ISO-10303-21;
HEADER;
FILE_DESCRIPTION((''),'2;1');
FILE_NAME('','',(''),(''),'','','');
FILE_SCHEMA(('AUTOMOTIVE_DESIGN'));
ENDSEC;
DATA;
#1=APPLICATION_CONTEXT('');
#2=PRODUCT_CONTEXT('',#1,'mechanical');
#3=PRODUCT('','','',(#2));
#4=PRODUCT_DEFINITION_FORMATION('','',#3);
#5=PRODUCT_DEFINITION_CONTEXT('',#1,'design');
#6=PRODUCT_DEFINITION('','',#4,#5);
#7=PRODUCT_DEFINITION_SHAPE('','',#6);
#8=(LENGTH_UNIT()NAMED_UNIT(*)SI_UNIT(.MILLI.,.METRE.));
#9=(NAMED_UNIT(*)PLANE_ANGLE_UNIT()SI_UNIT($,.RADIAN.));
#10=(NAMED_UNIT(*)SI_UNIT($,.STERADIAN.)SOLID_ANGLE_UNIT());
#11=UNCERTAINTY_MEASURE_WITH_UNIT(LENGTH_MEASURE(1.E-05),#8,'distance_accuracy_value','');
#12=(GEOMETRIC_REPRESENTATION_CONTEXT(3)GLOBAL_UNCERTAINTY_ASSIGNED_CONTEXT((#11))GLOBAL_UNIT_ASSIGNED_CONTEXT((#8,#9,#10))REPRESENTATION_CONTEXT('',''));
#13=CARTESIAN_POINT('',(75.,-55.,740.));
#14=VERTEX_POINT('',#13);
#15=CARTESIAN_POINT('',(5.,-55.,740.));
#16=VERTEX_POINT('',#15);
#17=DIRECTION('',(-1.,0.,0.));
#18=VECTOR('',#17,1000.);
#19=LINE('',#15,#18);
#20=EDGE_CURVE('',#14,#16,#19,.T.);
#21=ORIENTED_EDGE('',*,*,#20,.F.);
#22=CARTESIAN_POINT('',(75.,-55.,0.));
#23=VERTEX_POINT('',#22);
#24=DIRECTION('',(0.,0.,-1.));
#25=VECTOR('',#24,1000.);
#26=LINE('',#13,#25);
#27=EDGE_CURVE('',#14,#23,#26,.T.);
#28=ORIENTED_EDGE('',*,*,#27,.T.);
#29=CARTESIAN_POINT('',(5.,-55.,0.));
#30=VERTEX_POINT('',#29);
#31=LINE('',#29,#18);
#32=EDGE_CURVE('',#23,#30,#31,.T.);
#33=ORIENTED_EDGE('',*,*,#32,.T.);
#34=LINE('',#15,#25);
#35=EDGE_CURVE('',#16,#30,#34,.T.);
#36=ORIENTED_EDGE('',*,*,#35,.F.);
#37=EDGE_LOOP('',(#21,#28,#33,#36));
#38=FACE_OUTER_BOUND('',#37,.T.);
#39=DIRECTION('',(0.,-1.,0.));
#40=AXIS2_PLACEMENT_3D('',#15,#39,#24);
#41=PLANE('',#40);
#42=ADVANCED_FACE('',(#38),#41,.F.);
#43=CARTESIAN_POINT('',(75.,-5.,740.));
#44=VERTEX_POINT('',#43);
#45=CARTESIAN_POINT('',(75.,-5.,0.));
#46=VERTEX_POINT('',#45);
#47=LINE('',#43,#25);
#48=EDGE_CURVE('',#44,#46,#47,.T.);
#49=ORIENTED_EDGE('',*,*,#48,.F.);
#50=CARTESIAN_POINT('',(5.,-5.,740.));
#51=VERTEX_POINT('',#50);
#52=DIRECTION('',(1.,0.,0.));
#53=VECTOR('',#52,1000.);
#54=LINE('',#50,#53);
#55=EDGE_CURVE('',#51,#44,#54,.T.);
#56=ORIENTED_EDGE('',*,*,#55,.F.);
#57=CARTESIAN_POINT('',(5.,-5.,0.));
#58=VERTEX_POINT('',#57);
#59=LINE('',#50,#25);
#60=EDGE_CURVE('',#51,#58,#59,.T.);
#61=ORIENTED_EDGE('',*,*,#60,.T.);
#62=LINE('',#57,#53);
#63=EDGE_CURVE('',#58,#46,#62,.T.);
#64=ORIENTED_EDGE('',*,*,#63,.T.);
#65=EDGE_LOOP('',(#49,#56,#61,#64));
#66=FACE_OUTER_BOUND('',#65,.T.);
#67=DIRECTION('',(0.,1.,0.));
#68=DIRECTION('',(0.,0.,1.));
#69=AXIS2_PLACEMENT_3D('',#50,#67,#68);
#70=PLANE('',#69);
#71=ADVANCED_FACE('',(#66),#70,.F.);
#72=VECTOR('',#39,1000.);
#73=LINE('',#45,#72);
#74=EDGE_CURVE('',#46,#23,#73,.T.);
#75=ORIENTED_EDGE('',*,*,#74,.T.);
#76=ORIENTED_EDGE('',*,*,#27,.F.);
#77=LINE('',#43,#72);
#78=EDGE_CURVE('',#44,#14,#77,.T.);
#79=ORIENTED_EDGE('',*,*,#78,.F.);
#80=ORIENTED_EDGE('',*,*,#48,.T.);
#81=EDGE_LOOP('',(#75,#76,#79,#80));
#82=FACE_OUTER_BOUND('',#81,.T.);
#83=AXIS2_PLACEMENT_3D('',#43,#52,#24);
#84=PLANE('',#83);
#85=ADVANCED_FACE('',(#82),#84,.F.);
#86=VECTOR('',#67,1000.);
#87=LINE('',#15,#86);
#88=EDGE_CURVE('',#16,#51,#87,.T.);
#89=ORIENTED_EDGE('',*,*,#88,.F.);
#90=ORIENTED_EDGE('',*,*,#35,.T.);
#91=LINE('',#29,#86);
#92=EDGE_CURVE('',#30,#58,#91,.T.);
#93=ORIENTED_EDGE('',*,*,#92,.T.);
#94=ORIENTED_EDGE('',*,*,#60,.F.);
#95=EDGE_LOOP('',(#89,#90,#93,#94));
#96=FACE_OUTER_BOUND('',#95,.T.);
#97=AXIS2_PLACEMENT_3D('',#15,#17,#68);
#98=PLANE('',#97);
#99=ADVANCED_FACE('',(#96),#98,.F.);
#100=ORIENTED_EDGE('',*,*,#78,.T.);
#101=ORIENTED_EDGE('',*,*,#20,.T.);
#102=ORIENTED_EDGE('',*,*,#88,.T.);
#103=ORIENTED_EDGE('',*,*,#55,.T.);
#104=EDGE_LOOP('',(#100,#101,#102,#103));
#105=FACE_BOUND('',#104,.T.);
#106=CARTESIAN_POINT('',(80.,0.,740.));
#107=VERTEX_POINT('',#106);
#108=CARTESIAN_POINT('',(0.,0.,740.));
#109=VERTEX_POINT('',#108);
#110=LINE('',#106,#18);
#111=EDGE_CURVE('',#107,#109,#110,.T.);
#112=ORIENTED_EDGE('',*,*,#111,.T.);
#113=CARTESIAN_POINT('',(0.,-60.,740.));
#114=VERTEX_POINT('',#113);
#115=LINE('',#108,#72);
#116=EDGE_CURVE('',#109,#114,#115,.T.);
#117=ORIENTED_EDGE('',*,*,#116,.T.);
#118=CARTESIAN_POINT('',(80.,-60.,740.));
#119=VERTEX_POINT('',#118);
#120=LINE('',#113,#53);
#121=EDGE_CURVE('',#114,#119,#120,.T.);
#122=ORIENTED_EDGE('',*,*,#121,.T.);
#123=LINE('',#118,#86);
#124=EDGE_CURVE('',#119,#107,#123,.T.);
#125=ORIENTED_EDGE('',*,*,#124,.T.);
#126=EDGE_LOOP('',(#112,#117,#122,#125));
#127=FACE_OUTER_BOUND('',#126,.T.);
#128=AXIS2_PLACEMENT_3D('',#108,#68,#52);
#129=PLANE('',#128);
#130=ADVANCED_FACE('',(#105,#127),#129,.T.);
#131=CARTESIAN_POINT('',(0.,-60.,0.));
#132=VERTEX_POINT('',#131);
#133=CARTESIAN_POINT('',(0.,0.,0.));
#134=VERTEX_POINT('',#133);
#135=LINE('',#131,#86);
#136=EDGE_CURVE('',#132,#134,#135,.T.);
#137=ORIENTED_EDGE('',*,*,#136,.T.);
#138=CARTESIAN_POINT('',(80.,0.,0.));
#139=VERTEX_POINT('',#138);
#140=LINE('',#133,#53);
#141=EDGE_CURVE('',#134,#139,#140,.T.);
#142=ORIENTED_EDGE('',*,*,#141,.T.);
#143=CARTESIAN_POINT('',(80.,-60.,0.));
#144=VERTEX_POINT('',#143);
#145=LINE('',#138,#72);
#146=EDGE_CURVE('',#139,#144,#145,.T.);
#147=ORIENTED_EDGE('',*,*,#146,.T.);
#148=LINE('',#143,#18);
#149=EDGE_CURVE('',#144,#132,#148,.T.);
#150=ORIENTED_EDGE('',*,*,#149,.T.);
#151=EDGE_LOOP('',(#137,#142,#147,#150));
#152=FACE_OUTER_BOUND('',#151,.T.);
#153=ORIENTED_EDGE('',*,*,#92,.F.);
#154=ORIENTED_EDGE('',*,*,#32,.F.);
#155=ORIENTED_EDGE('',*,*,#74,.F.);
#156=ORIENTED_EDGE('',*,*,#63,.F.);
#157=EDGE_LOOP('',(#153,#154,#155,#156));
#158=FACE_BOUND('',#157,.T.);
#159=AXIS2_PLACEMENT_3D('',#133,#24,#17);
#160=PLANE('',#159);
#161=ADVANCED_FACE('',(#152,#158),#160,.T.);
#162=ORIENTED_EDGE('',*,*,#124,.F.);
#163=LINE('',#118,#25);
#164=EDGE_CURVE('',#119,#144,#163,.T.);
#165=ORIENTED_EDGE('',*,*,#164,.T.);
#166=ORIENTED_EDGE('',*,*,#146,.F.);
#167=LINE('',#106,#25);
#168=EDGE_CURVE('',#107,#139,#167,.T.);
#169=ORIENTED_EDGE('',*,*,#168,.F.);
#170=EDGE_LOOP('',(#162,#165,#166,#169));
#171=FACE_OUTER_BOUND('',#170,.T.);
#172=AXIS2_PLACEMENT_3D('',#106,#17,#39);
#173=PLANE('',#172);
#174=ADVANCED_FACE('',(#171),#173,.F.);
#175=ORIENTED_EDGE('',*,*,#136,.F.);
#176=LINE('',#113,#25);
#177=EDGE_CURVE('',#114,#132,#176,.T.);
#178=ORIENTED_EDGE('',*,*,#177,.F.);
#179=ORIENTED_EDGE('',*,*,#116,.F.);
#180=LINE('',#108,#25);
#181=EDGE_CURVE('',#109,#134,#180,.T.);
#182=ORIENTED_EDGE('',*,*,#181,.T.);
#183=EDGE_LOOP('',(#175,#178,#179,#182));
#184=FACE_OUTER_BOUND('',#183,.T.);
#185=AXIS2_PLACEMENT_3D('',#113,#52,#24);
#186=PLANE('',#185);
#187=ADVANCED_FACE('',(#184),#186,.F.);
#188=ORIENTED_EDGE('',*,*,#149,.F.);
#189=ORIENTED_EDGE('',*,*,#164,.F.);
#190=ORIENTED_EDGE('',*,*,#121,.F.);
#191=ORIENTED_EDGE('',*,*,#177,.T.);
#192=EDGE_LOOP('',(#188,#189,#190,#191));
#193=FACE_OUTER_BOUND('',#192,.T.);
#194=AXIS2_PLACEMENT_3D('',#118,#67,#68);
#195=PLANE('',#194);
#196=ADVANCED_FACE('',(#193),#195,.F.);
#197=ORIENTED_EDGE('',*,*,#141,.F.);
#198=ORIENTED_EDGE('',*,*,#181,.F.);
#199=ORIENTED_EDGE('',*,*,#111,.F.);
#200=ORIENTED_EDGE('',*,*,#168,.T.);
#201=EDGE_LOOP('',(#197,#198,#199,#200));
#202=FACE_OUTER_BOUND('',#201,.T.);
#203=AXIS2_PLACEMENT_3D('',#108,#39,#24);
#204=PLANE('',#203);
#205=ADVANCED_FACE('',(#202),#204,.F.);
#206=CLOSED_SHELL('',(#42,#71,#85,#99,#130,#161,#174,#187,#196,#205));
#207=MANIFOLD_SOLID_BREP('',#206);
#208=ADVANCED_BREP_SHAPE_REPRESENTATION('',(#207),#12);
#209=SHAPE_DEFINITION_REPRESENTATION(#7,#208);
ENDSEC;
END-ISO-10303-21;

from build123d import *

# Parameters (mm, degrees)
SKETCH_1_W          = 80
SKETCH_1_H          = 60
SKETCH_1_W_2        = 74
SKETCH_1_H_2        = 54
EXTRUDE_1_DEPTH     = 740
SKETCH_3_W          = 80
SKETCH_3_H          = 60
CUT_EXTRUDE_1_DEPTH = 25
SKETCH_4_W          = 80
SKETCH_4_H          = 60
CUT_EXTRUDE_2_DEPTH = 25
SKETCH_5_W          = 80
SKETCH_5_H          = 60
SKETCH_5_W_2        = 74
SKETCH_5_H_2        = 54
EXTRUDE_2_DEPTH     = 25
SKETCH_6_W          = 80
SKETCH_6_H          = 60
SKETCH_6_W_2        = 74
SKETCH_6_H_2        = 54
EXTRUDE_3_DEPTH     = 25
SKETCH_7_W          = 45
SKETCH_7_H          = 5
CUT_EXTRUDE_3_DEPTH = 80
EXTRUDE_4_DEPTH     = 45
EXTRUDE_5_DEPTH     = 45
SKETCH_10_W         = 74
SKETCH_10_H         = 54
SKETCH_10_W_2       = 70
SKETCH_10_H_2       = 50
EXTRUDE_6_DEPTH     = 740


with BuildPart() as part:
    # 草图1 → 凸台-拉伸1 (new body)
    with BuildSketch(Plane.XY):
        with Locations((40, -30)):
            Rectangle(SKETCH_1_W, SKETCH_1_H)
        with Locations((40, -30)):
            Rectangle(SKETCH_1_W_2, SKETCH_1_H_2, mode=Mode.SUBTRACT)
    extrude(amount=EXTRUDE_1_DEPTH)

    # 草图3 → 切除-拉伸1 (cut)
    with BuildSketch(Plane.XY.offset(740)):
        with Locations((40, -30)):
            Rectangle(SKETCH_3_W, SKETCH_3_H)
    extrude(amount=-CUT_EXTRUDE_1_DEPTH, mode=Mode.SUBTRACT)

    # 草图4 → 切除-拉伸2 (cut)
    with BuildSketch(Plane(origin=(0, 0, 0), x_dir=(-1, 0, 0), z_dir=(0, 0, -1))):
        with Locations((-40, -30)):
            Rectangle(SKETCH_4_W, SKETCH_4_H)
    extrude(amount=-CUT_EXTRUDE_2_DEPTH, mode=Mode.SUBTRACT)

    # 草图5 → 凸台-拉伸2 (add)
    with BuildSketch(Plane.XY.offset(715)):
        with Locations((40, -30)):
            Rectangle(SKETCH_5_W, SKETCH_5_H)
        with Locations((40, -30)):
            Rectangle(SKETCH_5_W_2, SKETCH_5_H_2, mode=Mode.SUBTRACT)
    extrude(amount=EXTRUDE_2_DEPTH)

    # 草图6 → 凸台-拉伸3 (add)
    with BuildSketch(Plane(origin=(0, 0, 25), x_dir=(-1, 0, 0), z_dir=(0, 0, -1))):
        with Locations((-40, -30)):
            Rectangle(SKETCH_6_W, SKETCH_6_H)
        with Locations((-40, -30)):
            Rectangle(SKETCH_6_W_2, SKETCH_6_H_2, mode=Mode.SUBTRACT)
    extrude(amount=EXTRUDE_3_DEPTH)

    # 草图7 → 切除-拉伸3 (cut)
    with BuildSketch(Plane(origin=(80, 0, 0), x_dir=(0, 0, -1), z_dir=(1, 0, 0))):
        with Locations((-717.5, -57.5)):
            Rectangle(SKETCH_7_W, SKETCH_7_H)
        with Locations((-22.5, -57.5)):
            Rectangle(SKETCH_7_W, SKETCH_7_H)
    extrude(amount=-CUT_EXTRUDE_3_DEPTH, mode=Mode.SUBTRACT)

    # 草图8 → 凸台-拉伸4 (add)
    with BuildSketch(Plane(origin=(0, 0, 45), x_dir=(-1, 0, 0), z_dir=(0, 0, -1))):
        Polygon((-3, -55), (-3, -57), (-77, -57), (-77, -55), (-80, -55), (-80, -60), (0, -60), (0, -55), align=None)
    extrude(amount=EXTRUDE_4_DEPTH)

    # 草图9 → 凸台-拉伸5 (add)
    with BuildSketch(Plane.XY.offset(695)):
        Polygon((3, -57), (3, -55), (0, -55), (0, -60), (80, -60), (80, -55), (77, -55), (77, -57), align=None)
    extrude(amount=EXTRUDE_5_DEPTH)

    # 草图10 → 凸台-拉伸6 (add)
    with BuildSketch(Plane(origin=(0, 0, 0), x_dir=(-1, 0, 0), z_dir=(0, 0, -1))):
        with Locations((-40, -30)):
            Rectangle(SKETCH_10_W, SKETCH_10_H)
        with Locations((-40, -30)):
            Rectangle(SKETCH_10_W_2, SKETCH_10_H_2, mode=Mode.SUBTRACT)
    extrude(amount=-EXTRUDE_6_DEPTH)


solid = part.part
